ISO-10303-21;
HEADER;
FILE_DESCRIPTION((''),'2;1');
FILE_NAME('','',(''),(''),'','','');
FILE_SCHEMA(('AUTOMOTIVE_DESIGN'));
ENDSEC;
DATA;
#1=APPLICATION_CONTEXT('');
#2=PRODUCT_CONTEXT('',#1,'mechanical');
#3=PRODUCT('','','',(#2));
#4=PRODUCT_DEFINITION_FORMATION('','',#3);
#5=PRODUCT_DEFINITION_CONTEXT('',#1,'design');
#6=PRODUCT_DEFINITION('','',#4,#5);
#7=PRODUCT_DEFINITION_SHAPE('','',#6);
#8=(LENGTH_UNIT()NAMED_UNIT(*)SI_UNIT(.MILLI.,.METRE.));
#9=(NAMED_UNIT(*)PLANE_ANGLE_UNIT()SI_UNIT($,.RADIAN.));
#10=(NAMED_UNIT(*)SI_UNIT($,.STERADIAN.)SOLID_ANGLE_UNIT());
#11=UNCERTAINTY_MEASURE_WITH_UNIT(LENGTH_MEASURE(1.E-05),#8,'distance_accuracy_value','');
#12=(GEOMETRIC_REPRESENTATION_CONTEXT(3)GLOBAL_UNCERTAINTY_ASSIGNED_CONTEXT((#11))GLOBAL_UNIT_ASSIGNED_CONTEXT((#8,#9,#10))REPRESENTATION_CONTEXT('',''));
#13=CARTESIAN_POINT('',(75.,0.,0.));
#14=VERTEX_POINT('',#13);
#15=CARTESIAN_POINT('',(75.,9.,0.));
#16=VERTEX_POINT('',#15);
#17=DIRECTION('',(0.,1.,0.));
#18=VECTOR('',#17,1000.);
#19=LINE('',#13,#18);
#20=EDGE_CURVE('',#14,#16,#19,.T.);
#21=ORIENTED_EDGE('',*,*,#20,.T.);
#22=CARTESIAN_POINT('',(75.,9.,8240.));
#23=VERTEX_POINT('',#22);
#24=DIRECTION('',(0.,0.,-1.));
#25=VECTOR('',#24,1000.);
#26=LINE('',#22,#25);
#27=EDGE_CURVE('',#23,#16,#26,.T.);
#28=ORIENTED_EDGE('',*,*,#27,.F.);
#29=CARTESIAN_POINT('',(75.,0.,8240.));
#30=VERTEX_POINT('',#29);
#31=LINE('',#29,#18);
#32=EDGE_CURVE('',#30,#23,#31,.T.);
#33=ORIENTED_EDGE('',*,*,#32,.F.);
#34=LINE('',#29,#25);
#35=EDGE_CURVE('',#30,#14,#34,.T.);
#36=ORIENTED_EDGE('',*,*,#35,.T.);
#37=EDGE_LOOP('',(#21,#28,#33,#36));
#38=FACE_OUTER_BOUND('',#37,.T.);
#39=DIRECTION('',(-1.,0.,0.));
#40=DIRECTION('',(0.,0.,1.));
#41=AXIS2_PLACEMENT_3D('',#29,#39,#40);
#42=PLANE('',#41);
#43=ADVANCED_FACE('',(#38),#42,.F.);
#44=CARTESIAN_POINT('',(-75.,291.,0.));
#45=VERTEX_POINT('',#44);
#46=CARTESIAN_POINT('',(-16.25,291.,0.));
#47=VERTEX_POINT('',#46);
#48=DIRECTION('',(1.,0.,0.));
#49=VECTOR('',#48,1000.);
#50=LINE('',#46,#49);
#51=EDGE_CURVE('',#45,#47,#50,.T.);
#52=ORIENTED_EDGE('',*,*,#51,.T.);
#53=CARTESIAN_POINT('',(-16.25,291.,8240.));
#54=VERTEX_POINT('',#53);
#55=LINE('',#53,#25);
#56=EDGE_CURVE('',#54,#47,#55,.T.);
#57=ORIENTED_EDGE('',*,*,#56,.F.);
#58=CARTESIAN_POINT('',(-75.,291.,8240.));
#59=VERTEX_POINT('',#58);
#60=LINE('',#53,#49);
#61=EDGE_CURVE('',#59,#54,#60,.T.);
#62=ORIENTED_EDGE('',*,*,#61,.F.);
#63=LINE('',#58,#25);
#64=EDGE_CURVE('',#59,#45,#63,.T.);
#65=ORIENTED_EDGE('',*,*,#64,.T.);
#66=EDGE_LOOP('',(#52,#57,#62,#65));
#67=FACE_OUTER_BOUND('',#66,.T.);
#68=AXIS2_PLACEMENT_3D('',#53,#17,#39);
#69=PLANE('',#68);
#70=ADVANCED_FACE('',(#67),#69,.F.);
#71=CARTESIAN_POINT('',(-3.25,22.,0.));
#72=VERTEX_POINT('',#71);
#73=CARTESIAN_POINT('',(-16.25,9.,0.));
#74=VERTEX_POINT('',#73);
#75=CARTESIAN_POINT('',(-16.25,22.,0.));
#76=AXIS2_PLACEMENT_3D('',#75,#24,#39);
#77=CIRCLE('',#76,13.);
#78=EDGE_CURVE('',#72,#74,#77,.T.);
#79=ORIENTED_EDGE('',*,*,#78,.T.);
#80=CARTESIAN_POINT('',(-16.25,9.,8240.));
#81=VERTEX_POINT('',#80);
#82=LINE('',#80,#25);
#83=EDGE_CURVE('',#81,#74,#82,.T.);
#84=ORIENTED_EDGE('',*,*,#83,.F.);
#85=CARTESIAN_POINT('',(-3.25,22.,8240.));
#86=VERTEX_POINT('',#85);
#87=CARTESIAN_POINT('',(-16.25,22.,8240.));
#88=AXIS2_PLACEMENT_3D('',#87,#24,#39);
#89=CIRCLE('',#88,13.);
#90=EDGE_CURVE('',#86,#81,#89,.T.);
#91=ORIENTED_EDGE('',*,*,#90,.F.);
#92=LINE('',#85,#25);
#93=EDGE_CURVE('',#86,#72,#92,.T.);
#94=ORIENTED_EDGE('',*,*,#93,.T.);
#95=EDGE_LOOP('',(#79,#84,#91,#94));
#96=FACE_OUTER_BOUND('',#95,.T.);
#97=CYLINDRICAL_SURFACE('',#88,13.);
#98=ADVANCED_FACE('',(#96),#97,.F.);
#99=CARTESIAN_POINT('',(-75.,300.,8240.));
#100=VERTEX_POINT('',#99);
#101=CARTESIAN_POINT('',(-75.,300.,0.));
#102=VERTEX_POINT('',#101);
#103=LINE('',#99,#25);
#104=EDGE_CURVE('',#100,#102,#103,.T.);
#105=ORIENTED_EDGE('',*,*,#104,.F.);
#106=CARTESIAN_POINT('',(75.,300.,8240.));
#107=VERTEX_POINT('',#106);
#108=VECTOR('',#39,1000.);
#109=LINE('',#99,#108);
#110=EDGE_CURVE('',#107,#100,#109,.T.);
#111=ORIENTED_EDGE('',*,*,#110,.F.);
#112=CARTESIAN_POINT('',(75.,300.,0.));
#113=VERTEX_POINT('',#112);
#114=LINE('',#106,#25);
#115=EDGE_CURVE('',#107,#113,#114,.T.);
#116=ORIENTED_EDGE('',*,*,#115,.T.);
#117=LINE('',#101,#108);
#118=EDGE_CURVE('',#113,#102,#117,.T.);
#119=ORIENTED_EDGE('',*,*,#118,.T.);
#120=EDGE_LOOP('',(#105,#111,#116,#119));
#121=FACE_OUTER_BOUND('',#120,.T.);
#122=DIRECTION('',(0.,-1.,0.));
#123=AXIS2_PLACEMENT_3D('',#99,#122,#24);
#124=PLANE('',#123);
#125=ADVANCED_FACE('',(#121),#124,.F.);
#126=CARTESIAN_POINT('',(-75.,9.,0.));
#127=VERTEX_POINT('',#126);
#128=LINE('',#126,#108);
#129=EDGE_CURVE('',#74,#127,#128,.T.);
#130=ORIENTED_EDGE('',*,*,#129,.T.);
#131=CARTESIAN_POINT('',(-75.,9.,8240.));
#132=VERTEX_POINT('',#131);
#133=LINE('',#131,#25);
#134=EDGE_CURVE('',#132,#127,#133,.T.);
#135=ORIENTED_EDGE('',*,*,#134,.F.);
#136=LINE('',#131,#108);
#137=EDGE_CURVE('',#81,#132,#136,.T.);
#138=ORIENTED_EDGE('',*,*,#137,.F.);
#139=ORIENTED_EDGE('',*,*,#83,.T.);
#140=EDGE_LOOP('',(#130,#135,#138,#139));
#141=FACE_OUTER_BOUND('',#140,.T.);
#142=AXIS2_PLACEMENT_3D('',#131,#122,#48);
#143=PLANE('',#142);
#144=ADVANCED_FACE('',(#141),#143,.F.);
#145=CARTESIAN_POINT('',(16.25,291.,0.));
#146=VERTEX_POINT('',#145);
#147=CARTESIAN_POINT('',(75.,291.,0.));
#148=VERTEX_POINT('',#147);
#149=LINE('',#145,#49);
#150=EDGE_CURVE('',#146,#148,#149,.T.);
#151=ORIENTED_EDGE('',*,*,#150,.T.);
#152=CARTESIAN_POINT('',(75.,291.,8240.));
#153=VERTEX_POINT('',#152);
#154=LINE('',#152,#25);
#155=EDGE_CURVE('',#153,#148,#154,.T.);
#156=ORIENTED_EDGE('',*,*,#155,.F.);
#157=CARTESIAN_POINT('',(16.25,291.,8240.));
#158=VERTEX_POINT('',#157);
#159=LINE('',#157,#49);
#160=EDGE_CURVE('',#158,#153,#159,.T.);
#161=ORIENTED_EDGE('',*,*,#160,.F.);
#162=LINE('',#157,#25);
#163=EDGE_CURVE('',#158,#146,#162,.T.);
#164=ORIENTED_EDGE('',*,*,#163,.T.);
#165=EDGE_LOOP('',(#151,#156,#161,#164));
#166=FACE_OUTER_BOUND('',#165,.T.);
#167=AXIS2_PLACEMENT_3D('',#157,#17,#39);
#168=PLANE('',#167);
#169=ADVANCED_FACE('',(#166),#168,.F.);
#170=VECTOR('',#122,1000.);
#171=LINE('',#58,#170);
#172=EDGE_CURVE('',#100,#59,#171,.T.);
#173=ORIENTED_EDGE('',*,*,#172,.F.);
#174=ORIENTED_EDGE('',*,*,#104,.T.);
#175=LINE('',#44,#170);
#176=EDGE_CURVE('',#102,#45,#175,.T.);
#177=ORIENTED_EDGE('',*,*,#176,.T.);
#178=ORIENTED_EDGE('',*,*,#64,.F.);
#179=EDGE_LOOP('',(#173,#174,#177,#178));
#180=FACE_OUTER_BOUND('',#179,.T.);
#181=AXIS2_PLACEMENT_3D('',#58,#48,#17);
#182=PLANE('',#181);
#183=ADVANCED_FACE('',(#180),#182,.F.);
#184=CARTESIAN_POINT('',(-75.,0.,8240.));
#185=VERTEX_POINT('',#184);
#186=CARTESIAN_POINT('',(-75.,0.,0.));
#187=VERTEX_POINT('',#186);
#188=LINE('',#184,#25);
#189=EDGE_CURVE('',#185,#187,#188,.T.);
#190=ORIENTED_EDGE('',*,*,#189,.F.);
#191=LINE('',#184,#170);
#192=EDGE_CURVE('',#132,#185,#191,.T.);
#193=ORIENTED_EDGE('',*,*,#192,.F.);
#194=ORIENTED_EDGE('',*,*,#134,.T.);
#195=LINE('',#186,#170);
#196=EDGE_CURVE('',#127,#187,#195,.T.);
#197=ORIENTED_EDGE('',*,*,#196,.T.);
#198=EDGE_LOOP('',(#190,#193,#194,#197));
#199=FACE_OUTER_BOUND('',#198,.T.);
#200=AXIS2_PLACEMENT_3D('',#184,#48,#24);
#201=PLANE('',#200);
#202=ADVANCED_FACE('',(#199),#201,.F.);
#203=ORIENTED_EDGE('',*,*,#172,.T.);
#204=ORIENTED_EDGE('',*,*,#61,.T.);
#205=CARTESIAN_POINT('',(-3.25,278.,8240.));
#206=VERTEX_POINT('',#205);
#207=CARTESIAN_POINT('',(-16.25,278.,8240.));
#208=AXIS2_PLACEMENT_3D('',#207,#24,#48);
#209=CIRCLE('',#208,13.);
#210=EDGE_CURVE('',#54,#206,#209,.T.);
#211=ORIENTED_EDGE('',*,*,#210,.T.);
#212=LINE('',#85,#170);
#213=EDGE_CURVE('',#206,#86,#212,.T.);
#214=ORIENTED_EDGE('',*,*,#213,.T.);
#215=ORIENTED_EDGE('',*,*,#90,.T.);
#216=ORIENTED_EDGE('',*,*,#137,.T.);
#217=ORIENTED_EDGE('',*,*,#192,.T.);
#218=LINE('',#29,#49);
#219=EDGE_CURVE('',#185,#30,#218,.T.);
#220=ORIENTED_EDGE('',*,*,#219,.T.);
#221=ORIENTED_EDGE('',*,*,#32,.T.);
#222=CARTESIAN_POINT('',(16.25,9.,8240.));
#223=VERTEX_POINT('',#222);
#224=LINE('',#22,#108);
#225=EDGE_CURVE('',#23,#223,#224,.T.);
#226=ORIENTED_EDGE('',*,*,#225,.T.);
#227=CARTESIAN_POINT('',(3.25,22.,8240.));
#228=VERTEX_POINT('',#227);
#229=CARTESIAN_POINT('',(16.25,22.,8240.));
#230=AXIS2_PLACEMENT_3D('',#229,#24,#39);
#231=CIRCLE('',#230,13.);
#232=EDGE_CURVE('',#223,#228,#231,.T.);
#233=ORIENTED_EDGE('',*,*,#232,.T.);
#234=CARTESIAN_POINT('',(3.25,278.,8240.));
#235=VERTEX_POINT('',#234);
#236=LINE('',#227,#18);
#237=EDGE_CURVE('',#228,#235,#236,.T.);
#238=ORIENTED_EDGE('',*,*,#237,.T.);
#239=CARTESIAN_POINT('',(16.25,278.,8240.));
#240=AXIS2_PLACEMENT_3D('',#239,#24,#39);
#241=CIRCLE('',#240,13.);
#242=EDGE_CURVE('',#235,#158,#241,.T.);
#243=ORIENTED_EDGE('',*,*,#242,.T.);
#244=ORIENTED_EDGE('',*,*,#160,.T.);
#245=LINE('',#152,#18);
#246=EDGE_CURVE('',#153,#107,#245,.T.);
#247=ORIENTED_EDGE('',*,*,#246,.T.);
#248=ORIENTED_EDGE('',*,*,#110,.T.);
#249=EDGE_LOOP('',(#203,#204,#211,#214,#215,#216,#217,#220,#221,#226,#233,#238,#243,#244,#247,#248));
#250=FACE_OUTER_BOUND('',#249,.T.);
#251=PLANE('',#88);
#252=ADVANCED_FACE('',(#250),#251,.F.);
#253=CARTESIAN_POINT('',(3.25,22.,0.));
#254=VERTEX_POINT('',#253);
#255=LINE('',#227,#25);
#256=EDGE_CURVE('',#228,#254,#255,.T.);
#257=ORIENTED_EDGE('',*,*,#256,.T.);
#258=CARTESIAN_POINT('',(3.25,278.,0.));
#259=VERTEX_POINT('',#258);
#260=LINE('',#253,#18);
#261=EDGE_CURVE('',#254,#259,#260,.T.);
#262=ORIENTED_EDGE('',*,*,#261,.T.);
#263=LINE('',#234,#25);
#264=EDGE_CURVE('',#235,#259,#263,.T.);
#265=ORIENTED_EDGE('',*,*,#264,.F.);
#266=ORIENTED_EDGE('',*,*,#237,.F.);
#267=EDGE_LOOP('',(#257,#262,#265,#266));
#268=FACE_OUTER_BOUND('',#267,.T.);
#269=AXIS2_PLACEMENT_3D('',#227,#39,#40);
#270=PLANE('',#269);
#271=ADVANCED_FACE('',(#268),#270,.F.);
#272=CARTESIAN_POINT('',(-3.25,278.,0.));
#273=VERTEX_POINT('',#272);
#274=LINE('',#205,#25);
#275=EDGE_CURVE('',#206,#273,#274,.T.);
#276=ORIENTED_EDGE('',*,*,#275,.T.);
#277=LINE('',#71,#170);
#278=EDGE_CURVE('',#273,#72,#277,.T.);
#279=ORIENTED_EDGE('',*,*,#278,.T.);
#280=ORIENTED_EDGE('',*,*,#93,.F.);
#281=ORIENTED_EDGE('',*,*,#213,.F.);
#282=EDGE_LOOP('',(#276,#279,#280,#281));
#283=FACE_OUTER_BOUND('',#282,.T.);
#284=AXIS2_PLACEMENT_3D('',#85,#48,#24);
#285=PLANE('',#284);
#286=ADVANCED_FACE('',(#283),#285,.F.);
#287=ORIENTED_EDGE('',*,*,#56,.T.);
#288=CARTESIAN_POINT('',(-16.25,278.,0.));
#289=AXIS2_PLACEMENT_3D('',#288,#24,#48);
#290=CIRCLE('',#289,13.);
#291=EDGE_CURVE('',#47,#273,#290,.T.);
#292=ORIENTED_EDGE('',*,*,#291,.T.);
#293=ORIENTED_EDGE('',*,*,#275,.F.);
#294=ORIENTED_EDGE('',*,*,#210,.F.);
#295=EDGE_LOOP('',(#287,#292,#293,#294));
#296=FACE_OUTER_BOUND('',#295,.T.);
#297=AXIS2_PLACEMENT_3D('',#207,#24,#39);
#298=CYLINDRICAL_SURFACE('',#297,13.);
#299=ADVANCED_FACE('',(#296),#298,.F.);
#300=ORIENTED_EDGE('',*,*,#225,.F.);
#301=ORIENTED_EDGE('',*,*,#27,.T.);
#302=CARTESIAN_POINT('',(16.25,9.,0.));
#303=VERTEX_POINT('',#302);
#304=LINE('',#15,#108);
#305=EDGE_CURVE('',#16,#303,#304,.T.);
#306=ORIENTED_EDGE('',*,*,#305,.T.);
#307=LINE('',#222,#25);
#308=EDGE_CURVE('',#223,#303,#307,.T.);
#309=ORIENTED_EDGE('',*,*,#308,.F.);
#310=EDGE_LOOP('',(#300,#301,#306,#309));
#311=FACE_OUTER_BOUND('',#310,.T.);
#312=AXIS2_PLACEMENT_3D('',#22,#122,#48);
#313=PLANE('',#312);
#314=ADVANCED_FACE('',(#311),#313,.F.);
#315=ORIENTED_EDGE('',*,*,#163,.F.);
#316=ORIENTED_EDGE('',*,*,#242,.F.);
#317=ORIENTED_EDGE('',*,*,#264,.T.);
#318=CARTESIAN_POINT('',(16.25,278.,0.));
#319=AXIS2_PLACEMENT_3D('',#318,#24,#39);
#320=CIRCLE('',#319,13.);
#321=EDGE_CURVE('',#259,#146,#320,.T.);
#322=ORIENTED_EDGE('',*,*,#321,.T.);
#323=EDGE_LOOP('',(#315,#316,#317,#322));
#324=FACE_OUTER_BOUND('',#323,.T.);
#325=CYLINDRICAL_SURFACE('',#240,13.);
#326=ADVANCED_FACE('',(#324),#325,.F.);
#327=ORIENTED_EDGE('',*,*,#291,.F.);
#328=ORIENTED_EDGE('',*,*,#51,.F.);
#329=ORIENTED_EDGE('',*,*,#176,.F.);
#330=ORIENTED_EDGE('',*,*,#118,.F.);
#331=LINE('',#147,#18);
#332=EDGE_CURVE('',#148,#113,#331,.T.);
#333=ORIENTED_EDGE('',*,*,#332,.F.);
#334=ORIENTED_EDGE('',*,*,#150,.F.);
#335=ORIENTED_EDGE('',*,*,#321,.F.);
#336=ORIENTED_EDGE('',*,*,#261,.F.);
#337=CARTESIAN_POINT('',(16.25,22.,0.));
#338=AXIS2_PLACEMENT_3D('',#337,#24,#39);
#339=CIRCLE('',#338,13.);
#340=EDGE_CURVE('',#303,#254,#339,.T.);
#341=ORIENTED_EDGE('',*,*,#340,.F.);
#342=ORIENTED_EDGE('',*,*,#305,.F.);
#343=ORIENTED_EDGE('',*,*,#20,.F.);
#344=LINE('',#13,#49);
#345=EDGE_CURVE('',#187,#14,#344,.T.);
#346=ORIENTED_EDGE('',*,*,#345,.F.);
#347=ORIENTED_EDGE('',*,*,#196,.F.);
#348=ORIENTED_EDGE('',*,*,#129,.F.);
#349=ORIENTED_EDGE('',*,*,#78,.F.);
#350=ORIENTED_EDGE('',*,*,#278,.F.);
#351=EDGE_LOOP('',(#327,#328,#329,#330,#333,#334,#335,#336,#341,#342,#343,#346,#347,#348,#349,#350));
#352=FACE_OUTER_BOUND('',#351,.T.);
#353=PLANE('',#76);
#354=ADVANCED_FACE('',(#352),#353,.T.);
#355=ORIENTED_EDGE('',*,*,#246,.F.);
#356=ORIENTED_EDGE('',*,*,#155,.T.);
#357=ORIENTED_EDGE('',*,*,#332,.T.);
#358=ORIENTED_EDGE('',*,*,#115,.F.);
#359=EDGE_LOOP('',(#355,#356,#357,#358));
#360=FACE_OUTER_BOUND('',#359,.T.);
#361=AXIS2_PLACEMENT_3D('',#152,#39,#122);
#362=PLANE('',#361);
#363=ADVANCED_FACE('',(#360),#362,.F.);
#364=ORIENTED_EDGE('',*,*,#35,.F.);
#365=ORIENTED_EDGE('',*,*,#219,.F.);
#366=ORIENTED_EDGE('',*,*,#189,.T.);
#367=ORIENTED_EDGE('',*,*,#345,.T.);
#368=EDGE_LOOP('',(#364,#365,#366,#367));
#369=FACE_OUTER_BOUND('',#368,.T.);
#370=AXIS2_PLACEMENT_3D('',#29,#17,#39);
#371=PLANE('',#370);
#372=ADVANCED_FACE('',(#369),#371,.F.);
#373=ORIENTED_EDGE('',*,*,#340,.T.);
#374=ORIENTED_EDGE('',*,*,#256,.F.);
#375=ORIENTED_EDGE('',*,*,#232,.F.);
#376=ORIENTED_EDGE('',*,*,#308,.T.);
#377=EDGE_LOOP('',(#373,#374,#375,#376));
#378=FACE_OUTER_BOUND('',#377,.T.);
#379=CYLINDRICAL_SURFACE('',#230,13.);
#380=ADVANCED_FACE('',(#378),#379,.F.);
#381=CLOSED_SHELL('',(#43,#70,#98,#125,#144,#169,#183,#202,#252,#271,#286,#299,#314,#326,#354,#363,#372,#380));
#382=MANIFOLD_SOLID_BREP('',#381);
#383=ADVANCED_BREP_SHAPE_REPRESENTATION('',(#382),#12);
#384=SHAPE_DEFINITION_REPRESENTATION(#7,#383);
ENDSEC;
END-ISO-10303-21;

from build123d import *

# Parameters (mm, degrees)
BOSS_EXTRUDE1_DEPTH = 8240


with BuildPart() as part:
    # Sketch1 → Boss-Extrude1 (new body)
    with BuildSketch(Plane.XY):
        with BuildLine():
            Line((75, 0), (-75, 0))
            Line((-75, 0), (-75, 9))
            Line((-75, 9), (-16.25, 9))
            ThreePointArc((-16.25, 9), (-7.057611845, 12.807611845), (-3.25, 22))
            Line((-3.25, 22), (-3.25, 278))
            ThreePointArc((-3.25, 278), (-7.057611845, 287.192388155), (-16.25, 291))
            Line((-16.25, 291), (-75, 291))
            Line((-75, 291), (-75, 300))
            Line((-75, 300), (75, 300))
            Line((75, 300), (75, 291))
            Line((75, 291), (16.25, 291))
            ThreePointArc((16.25, 291), (7.057611845, 287.192388155), (3.25, 278))
            Line((3.25, 278), (3.25, 22))
            ThreePointArc((3.25, 22), (7.057611845, 12.807611845), (16.25, 9))
            Line((16.25, 9), (75, 9))
            Line((75, 9), (75, 0))
        make_face()
    extrude(amount=BOSS_EXTRUDE1_DEPTH)


solid = part.part
